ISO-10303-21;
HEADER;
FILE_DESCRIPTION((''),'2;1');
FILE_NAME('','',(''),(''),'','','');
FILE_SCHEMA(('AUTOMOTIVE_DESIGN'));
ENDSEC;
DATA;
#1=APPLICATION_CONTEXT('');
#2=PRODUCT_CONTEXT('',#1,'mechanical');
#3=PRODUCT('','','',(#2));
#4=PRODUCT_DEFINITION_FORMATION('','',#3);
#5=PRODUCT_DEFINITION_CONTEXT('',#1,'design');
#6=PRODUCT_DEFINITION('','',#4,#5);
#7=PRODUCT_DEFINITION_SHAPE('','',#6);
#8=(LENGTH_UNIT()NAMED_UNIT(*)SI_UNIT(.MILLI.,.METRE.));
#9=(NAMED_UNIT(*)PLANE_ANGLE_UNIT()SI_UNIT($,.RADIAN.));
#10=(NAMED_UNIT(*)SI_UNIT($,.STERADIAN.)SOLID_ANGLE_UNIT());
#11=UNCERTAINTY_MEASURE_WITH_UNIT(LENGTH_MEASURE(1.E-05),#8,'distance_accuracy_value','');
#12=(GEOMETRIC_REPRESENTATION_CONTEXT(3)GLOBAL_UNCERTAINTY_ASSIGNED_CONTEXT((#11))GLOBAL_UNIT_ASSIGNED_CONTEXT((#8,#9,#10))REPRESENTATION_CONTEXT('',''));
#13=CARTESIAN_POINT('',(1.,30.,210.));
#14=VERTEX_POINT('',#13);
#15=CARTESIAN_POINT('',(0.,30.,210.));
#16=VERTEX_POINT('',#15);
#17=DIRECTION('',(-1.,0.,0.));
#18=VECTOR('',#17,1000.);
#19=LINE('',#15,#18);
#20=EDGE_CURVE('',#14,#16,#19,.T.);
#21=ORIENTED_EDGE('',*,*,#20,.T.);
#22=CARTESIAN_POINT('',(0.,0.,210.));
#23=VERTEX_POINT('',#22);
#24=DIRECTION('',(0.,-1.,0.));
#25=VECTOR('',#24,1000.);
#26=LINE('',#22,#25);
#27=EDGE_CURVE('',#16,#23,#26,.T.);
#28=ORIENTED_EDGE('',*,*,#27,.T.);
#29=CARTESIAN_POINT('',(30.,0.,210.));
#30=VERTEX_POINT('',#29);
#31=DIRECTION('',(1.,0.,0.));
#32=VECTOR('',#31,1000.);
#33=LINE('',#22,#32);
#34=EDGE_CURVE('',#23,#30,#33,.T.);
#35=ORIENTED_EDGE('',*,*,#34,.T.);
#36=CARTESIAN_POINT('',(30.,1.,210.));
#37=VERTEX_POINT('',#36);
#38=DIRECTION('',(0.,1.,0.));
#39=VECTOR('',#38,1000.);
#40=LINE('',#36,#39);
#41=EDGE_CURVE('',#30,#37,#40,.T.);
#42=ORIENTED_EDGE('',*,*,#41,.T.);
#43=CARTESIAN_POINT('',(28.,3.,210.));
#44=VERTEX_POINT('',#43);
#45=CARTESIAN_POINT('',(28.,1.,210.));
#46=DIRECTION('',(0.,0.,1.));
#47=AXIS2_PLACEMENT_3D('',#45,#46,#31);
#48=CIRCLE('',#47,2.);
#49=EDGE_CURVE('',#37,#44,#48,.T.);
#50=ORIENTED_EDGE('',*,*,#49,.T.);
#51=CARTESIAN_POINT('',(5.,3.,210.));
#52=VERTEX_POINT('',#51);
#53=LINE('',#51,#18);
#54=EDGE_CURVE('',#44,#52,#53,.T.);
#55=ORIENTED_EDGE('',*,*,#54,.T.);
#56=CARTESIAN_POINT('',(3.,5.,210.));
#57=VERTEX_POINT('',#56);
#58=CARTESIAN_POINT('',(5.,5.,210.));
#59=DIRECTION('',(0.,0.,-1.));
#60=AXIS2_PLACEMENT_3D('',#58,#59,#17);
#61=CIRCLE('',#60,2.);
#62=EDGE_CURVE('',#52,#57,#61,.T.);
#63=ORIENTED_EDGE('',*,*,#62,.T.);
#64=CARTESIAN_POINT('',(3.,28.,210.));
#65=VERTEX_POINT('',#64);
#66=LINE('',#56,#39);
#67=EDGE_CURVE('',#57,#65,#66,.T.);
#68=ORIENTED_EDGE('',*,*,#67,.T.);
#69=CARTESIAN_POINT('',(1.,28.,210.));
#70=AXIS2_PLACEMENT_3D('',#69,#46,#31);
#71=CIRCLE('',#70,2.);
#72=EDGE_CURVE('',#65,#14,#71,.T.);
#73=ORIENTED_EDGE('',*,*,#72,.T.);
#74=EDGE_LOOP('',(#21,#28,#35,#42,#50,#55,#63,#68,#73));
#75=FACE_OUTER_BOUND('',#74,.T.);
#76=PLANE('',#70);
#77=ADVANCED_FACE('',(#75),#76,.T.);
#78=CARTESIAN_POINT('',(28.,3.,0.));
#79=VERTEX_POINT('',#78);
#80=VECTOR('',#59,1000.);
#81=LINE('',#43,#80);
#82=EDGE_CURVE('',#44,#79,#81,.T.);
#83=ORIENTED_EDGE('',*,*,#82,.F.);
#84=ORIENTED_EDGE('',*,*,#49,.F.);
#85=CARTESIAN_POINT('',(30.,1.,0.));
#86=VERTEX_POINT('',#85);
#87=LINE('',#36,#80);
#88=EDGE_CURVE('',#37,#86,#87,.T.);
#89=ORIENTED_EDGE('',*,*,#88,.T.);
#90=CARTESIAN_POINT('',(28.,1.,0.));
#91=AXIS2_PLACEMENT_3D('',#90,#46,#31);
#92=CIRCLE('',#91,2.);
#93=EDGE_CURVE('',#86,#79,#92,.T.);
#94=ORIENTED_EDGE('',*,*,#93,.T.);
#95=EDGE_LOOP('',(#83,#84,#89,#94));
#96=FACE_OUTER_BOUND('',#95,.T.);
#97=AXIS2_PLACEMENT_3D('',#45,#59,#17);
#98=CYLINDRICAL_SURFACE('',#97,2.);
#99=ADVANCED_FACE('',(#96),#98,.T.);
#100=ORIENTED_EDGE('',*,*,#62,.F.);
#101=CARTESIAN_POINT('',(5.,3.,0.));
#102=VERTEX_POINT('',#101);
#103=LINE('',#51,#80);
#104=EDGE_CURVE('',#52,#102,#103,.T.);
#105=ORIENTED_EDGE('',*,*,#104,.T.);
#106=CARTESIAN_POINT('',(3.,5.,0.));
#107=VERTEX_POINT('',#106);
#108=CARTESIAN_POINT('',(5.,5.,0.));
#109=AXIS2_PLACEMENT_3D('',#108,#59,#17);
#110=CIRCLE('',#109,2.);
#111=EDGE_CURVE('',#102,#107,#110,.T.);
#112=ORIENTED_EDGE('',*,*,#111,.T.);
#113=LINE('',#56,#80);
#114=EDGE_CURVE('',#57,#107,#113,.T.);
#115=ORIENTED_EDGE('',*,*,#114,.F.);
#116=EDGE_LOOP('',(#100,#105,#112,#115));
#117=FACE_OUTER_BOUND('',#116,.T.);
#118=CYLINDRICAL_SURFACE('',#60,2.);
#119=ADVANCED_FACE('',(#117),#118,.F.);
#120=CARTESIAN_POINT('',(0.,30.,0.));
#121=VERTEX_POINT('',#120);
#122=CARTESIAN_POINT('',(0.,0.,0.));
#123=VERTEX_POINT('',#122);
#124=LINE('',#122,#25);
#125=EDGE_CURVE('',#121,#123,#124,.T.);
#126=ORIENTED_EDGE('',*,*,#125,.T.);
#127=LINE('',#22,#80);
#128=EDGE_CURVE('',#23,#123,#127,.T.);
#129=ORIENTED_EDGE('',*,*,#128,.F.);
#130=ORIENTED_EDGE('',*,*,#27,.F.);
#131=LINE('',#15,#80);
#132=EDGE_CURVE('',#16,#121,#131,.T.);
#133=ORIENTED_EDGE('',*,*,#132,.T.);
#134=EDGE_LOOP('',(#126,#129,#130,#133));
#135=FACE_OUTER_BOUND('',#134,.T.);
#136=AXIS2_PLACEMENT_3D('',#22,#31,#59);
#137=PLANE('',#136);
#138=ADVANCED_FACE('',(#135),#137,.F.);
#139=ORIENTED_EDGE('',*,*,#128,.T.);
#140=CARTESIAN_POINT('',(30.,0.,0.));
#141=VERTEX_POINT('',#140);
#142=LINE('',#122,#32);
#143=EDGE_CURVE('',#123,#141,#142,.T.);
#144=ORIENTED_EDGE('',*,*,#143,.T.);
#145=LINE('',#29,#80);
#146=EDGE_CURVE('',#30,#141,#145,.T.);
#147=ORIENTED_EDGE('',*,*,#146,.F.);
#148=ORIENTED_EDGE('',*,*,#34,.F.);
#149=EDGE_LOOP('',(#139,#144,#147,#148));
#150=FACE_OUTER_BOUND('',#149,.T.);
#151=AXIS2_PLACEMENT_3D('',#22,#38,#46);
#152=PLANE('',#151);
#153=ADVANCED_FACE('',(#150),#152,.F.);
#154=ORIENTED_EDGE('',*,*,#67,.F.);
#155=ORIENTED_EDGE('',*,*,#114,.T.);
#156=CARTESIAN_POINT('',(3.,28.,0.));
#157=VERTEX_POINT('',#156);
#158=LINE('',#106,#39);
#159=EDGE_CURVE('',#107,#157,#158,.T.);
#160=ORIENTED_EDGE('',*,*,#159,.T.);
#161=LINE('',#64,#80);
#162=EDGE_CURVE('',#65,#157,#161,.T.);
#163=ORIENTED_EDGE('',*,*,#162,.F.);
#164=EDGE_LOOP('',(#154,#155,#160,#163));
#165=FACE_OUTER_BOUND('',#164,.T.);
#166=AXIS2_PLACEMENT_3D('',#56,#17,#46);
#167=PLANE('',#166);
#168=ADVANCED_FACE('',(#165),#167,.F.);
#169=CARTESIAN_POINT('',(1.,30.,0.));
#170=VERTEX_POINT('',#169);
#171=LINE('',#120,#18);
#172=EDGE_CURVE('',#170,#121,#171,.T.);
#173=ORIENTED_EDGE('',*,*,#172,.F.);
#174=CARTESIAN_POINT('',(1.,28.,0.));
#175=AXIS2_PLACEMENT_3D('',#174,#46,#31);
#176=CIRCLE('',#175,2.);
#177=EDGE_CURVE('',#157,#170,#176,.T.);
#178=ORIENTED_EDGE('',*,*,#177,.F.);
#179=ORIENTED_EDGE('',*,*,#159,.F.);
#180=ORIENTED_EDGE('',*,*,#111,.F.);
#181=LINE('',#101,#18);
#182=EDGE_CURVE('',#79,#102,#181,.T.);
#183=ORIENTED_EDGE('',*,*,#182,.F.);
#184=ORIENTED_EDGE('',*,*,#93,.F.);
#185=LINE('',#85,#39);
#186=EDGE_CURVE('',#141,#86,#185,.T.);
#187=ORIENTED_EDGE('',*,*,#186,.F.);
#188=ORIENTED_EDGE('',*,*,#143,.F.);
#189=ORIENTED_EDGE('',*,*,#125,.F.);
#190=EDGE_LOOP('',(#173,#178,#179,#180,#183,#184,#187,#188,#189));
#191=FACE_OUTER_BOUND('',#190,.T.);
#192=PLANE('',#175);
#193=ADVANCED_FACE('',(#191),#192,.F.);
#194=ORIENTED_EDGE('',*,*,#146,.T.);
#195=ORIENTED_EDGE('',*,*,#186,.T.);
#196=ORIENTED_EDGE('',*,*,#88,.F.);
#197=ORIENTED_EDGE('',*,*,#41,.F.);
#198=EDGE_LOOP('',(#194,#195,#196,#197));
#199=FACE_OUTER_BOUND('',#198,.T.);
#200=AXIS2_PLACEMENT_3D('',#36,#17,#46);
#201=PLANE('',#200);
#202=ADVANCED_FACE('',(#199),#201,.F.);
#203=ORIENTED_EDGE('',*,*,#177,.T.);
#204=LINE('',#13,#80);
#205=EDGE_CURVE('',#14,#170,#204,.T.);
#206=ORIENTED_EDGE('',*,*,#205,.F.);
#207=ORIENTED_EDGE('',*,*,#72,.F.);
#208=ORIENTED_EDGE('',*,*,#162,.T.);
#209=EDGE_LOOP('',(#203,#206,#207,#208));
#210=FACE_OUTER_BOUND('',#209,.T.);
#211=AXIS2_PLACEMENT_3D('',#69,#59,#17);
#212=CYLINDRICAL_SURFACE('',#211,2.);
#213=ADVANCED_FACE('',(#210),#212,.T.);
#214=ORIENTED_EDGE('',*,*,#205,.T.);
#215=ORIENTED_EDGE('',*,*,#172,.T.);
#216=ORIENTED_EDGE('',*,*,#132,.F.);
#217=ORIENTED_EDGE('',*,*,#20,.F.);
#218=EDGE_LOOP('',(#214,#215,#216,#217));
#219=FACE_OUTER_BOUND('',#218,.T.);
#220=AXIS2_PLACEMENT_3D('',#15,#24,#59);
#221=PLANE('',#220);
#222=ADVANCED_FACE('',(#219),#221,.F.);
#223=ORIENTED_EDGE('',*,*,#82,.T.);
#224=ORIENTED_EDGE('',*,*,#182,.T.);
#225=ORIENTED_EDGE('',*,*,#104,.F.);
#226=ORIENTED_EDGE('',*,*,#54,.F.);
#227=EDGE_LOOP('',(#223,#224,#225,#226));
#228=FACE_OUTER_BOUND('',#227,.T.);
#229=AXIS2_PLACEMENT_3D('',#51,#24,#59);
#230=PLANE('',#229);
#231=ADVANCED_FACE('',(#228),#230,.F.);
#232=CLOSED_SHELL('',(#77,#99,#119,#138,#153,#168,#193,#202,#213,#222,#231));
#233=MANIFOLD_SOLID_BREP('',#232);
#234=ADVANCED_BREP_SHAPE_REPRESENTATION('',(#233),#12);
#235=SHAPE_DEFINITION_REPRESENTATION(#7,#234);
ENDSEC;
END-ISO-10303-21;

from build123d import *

# Parameters (mm, degrees)
BOSS_EXTRUDE1_DEPTH = 210


with BuildPart() as part:
    # Sketch1 → Boss-Extrude1 (new body)
    with BuildSketch(Plane.XY):
        with BuildLine():
            Line((0, 0), (30, 0))
            Line((30, 0), (30, 1))
            ThreePointArc((30, 1), (29.414213562, 2.414213562), (28, 3))
            Line((28, 3), (5, 3))
            ThreePointArc((5, 3), (3.585786438, 3.585786438), (3, 5))
            Line((3, 5), (3, 28))
            ThreePointArc((3, 28), (2.414213562, 29.414213562), (1, 30))
            Line((1, 30), (0, 30))
            Line((0, 30), (0, 0))
        make_face()
    extrude(amount=BOSS_EXTRUDE1_DEPTH)


solid = part.part
